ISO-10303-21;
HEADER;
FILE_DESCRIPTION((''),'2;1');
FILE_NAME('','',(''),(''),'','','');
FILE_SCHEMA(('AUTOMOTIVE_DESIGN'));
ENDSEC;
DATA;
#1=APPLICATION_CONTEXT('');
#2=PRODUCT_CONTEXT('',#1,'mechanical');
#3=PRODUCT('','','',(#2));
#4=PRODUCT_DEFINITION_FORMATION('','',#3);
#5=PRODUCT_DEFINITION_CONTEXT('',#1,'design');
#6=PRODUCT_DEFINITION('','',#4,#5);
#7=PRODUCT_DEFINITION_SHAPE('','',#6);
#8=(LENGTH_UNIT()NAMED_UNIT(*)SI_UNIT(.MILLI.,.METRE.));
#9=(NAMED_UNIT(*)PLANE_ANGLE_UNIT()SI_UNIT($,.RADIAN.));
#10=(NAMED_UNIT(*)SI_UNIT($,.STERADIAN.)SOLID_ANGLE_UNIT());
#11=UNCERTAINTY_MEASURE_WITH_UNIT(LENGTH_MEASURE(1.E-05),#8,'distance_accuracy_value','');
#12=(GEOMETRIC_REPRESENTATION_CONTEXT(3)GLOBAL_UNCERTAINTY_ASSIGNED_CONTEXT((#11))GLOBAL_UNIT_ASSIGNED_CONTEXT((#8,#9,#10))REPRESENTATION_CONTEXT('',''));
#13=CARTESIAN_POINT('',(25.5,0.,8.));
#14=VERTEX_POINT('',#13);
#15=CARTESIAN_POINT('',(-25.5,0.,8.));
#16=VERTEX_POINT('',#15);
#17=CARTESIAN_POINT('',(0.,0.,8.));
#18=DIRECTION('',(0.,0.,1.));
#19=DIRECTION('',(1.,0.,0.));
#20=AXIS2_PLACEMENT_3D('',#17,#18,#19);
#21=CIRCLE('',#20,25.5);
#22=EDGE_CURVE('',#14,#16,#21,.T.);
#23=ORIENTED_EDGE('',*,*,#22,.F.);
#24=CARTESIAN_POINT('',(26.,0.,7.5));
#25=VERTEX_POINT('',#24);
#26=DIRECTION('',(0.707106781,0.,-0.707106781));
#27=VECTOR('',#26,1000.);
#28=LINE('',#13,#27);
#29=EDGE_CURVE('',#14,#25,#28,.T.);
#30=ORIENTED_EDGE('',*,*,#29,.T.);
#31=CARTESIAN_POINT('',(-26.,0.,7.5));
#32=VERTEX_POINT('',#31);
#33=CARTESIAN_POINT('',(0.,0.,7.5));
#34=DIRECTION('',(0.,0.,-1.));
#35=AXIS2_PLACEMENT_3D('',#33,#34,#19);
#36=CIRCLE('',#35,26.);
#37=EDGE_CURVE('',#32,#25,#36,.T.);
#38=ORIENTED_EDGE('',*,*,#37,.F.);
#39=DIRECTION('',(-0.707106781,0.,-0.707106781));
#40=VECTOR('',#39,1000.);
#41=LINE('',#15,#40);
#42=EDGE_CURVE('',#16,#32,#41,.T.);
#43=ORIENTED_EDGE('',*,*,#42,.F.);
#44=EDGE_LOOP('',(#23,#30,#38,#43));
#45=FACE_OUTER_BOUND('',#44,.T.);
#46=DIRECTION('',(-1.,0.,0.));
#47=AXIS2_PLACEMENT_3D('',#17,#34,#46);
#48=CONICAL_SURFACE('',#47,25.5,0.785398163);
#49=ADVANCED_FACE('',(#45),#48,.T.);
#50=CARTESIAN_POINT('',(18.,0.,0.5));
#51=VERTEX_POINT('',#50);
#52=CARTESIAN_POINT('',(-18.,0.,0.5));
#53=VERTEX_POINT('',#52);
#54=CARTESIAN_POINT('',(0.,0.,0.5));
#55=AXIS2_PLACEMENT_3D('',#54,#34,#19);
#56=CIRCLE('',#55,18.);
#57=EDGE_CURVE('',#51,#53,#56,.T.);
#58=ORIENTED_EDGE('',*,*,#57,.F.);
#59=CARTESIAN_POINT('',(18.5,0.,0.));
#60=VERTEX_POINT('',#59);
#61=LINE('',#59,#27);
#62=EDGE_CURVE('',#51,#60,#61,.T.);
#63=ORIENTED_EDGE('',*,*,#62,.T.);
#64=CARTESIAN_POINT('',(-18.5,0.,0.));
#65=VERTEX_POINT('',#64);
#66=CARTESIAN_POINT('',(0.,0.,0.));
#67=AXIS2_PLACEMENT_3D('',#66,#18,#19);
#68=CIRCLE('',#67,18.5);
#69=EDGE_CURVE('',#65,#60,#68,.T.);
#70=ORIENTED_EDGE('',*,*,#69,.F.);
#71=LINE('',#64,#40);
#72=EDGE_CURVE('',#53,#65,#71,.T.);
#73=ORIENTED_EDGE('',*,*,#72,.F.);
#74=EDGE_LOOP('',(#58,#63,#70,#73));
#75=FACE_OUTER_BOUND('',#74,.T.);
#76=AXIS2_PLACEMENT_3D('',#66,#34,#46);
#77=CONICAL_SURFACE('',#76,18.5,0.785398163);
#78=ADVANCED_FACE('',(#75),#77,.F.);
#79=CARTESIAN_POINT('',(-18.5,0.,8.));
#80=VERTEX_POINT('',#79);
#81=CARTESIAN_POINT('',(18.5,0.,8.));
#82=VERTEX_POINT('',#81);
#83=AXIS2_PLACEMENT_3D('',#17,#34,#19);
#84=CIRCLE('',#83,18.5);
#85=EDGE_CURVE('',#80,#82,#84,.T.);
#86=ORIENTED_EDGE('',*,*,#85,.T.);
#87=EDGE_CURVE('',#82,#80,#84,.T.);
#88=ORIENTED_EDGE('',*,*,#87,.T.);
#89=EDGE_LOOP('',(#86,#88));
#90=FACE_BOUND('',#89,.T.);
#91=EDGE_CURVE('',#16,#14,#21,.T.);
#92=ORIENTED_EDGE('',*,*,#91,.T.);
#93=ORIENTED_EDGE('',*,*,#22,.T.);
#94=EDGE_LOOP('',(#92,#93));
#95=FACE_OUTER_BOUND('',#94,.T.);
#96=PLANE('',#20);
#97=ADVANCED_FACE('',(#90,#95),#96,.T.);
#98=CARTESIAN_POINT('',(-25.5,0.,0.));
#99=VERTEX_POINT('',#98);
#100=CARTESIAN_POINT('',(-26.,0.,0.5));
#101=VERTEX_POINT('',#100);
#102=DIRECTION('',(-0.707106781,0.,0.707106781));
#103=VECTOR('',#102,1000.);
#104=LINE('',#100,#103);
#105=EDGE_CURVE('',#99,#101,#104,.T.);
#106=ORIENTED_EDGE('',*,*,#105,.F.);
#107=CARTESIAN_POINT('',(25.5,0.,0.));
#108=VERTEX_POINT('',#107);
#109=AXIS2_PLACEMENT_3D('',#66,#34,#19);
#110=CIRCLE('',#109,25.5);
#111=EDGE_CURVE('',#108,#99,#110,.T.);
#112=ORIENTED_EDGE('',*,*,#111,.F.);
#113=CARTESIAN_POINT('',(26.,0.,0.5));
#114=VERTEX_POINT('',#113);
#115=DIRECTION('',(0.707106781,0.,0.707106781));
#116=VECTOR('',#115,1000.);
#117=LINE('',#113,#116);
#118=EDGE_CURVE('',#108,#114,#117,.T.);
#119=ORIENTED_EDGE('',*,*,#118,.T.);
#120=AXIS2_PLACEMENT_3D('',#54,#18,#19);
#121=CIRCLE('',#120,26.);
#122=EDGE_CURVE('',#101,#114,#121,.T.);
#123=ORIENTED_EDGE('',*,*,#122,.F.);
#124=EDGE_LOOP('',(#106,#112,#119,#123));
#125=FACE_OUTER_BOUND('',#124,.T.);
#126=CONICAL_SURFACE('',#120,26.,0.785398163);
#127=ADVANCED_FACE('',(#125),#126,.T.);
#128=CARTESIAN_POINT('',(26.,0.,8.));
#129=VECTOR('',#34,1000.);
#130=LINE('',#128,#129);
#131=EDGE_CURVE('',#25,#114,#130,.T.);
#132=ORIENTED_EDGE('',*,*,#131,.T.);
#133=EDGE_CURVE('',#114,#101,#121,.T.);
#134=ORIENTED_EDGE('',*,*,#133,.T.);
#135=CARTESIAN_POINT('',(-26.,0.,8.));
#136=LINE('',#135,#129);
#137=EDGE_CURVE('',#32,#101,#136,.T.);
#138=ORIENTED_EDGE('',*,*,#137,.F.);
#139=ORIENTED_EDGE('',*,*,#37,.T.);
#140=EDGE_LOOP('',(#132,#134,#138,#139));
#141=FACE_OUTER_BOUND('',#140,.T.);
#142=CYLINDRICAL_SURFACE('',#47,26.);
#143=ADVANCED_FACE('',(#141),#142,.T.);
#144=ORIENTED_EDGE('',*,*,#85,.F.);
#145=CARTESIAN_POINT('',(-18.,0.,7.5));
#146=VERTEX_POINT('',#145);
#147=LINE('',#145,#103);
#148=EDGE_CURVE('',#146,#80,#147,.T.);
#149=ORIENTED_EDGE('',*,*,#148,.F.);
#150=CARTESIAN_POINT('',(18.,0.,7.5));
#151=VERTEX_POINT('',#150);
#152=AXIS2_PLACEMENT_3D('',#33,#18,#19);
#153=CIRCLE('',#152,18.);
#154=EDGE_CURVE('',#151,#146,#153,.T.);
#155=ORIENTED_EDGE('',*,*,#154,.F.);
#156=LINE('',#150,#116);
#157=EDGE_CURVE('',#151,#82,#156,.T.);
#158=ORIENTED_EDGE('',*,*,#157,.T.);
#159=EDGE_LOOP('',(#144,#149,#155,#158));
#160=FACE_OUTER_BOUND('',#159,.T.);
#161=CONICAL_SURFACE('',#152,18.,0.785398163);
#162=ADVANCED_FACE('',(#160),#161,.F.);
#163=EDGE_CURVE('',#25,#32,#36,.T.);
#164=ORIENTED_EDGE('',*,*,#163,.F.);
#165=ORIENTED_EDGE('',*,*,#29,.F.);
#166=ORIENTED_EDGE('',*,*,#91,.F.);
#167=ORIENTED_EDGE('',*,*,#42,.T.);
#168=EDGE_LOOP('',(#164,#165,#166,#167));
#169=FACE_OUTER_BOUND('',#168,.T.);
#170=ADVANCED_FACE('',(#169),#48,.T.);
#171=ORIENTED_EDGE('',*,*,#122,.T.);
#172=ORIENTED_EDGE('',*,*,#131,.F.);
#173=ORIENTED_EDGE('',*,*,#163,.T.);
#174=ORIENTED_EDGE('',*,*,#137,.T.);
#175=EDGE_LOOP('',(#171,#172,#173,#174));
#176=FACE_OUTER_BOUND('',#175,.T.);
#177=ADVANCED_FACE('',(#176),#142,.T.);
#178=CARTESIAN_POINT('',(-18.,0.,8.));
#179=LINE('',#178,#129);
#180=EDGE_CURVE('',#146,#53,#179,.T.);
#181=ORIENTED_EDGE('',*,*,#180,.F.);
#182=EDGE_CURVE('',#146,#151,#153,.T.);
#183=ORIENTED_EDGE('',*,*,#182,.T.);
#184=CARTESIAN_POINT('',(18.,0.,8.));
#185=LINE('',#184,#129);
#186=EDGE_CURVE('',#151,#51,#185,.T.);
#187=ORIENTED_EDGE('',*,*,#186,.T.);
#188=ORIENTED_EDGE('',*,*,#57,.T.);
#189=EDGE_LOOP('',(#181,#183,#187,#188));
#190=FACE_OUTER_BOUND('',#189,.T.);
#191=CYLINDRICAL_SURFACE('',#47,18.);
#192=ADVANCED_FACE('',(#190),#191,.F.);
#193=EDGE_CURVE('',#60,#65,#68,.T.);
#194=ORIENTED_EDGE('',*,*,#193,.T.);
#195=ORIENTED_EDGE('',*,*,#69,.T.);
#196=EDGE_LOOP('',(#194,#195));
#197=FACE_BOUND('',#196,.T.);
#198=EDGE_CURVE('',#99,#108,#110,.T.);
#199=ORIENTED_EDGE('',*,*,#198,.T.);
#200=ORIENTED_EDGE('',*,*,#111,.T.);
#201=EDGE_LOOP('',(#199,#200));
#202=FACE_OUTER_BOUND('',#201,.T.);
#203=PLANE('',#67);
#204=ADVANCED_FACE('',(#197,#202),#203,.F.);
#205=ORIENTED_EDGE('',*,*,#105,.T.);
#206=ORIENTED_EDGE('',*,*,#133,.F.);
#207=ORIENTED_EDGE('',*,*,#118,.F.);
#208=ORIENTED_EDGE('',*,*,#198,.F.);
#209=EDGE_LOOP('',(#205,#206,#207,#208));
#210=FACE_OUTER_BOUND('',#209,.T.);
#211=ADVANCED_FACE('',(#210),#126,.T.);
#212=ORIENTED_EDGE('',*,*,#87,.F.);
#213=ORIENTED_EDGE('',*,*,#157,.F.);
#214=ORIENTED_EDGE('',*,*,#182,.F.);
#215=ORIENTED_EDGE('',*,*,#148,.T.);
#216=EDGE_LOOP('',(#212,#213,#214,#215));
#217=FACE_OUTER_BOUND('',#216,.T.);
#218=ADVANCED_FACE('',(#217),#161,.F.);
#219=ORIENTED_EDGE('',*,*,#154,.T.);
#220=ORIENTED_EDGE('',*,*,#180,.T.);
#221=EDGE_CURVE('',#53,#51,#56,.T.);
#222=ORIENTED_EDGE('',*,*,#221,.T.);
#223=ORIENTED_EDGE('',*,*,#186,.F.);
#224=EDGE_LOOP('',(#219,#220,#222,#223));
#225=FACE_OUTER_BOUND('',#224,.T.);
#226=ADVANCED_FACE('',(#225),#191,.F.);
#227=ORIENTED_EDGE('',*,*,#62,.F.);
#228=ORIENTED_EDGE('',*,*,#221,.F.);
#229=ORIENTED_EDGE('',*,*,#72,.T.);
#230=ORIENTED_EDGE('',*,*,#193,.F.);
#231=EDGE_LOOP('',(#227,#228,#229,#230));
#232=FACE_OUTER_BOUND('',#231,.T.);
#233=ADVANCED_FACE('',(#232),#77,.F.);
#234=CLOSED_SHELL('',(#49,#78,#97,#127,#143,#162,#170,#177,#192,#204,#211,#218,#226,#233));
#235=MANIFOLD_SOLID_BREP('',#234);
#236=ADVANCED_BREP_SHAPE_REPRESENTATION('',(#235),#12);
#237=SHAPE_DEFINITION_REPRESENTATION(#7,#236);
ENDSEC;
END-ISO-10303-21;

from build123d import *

# Parameters (mm, degrees)
SKETCH1_R           = 26
SKETCH1_R_2         = 18
BOSS_EXTRUDE1_DEPTH = 8
CHAMFER1_SIZE       = 0.5


with BuildPart() as part:
    # Sketch1 → Boss-Extrude1 (new body)
    with BuildSketch(Plane.XY):
        Circle(SKETCH1_R)
        Circle(SKETCH1_R_2, mode=Mode.SUBTRACT)
    extrude(amount=BOSS_EXTRUDE1_DEPTH)

    # Chamfer1
    chamfer1_edges = [part.edges().sort_by_distance(p)[0] for p in [
        (-26, 0, 0),
        (-26, 0, 8),
        (-18, 0, 0),
        (-18, 0, 8),
    ]]
    chamfer(chamfer1_edges, length=CHAMFER1_SIZE)


solid = part.part
